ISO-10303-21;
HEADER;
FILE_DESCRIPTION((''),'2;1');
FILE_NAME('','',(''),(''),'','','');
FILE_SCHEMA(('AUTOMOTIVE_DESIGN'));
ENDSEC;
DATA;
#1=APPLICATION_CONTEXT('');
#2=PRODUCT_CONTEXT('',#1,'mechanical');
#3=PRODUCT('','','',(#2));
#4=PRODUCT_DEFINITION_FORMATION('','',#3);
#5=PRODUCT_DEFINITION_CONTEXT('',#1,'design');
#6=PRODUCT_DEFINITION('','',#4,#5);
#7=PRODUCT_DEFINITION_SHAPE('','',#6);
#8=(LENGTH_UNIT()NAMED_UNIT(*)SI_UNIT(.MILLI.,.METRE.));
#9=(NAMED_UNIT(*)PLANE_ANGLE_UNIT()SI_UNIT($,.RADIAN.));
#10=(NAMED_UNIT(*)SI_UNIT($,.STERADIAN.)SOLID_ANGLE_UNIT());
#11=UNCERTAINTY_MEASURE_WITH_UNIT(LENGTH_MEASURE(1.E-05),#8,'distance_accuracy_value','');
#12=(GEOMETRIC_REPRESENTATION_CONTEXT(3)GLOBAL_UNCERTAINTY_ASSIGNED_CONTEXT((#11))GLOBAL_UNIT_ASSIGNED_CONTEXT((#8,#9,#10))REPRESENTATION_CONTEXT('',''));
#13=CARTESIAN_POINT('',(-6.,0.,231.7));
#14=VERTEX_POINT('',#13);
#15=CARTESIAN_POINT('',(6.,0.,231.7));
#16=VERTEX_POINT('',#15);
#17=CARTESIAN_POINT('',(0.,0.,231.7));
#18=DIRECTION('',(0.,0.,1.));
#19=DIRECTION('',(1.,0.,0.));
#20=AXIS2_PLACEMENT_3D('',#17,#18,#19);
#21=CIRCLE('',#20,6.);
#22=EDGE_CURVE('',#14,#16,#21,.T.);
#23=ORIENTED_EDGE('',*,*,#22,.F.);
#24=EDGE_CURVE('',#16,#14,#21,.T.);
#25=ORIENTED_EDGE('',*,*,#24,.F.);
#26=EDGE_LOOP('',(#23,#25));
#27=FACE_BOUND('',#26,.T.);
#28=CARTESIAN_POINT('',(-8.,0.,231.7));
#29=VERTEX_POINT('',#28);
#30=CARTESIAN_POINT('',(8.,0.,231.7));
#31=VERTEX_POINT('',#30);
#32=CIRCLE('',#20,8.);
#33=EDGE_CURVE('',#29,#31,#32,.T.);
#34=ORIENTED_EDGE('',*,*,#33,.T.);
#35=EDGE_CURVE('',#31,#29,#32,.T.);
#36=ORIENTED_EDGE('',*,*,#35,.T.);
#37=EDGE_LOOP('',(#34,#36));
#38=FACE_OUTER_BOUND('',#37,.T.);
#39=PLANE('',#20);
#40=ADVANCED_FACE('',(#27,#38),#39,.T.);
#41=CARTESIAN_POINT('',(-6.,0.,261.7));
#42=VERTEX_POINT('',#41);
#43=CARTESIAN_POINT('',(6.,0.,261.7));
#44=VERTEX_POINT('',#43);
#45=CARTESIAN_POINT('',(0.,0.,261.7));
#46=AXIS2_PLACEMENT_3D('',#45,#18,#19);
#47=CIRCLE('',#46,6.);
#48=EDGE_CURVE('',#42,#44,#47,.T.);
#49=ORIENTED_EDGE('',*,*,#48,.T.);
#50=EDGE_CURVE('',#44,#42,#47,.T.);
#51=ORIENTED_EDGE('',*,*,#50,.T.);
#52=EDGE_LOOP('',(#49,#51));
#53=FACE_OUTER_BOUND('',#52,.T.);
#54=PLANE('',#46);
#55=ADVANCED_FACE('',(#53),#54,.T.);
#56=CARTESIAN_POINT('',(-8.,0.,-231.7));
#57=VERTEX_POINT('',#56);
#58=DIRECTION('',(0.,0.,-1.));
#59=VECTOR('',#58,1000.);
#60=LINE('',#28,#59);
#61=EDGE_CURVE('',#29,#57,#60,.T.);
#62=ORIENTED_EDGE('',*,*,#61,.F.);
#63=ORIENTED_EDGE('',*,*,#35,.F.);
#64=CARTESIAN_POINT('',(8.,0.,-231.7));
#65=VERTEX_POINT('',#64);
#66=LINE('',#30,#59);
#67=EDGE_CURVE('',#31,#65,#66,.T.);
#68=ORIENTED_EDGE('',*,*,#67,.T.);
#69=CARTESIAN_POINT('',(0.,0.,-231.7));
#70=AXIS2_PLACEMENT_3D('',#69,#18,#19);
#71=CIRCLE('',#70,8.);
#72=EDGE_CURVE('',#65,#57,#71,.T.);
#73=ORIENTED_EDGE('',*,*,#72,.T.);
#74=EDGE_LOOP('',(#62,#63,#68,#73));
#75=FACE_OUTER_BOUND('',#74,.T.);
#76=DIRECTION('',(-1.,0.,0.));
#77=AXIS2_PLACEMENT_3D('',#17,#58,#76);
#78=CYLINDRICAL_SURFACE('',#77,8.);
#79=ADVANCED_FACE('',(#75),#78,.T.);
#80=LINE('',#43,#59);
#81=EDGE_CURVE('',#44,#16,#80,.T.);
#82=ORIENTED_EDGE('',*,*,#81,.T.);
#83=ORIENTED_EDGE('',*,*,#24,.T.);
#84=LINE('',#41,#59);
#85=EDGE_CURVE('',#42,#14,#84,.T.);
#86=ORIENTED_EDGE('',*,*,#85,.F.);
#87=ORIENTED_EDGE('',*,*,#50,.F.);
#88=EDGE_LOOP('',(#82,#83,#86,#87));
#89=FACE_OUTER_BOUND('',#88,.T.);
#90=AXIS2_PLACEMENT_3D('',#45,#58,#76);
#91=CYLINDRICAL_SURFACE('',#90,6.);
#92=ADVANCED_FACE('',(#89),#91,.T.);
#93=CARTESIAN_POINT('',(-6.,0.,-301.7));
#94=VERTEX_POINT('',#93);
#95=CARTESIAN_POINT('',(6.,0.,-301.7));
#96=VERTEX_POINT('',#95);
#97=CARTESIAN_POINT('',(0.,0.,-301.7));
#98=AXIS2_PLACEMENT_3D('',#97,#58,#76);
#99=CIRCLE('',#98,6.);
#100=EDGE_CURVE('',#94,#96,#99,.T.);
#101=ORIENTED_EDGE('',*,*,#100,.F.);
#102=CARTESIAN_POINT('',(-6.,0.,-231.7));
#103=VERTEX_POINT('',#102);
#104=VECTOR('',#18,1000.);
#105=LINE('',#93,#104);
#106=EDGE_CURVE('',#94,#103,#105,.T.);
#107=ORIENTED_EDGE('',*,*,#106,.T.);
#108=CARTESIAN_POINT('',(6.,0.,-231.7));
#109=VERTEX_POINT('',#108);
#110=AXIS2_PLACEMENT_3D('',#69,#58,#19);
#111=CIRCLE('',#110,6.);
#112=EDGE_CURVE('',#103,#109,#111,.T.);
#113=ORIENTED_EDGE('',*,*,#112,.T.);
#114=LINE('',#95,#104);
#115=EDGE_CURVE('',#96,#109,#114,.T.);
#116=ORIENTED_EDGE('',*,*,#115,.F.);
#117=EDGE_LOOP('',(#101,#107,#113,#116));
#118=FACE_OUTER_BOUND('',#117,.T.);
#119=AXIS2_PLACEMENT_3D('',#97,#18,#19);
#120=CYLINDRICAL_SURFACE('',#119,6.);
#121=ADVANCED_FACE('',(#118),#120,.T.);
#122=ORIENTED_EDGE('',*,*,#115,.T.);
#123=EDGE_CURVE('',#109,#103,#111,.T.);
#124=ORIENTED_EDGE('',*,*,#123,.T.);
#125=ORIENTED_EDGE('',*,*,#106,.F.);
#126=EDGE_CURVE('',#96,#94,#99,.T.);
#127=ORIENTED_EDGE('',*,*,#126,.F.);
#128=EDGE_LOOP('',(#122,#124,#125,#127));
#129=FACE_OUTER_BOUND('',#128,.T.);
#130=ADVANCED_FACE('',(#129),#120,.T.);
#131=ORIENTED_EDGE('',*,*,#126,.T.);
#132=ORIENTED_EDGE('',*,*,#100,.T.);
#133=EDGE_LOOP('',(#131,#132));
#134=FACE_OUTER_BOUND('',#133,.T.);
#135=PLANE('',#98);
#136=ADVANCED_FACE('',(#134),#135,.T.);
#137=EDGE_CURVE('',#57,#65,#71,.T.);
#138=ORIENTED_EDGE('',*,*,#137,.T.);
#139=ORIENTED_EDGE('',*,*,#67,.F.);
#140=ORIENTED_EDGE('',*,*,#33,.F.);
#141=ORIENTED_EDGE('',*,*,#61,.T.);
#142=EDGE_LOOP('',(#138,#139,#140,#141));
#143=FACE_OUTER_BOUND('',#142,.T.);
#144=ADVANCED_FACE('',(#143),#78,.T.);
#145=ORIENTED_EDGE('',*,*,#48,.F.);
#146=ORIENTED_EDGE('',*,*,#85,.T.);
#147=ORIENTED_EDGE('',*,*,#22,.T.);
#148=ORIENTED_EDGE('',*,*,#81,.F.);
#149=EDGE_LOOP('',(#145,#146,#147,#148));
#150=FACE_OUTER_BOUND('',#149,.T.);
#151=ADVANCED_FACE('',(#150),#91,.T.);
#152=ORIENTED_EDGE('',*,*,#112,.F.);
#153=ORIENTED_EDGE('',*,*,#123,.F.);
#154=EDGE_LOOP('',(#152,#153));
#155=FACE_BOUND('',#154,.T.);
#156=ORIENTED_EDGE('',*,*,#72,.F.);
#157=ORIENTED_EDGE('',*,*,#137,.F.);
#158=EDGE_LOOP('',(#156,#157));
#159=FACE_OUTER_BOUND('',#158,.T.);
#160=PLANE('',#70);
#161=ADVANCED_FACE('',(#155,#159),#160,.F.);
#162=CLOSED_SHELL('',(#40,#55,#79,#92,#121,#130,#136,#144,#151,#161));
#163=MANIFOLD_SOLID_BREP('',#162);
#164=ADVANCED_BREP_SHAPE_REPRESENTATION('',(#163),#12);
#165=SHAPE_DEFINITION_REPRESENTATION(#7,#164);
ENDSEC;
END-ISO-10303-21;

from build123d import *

# Parameters (mm, degrees)
SKETCH1_R           = 8
BOSS_EXTRUDE1_DEPTH = 231.7
SKETCH2_R           = 6
BOSS_EXTRUDE2_DEPTH = 30
BOSS_EXTRUDE3_START = 70
SKETCH4_R           = 6
BOSS_EXTRUDE3_DEPTH = 70


with BuildPart() as part:
    # Sketch1 → Boss-Extrude1 (new, symmetric)
    with BuildSketch(Plane.XY):
        with Locations(Location((0, 0, 0), (0, 0, 180))):
            Circle(SKETCH1_R)
    extrude(amount=BOSS_EXTRUDE1_DEPTH, both=True)

    # Sketch2 → Boss-Extrude2 (add)
    with BuildSketch(Plane.XY.offset(231.7)):
        Circle(SKETCH2_R)
    extrude(amount=BOSS_EXTRUDE2_DEPTH)

    # Sketch4 → Boss-Extrude3 (add)
    with BuildSketch(Plane(origin=(0, 0, -231.7), x_dir=(-1, 0, 0), z_dir=(0, 0, -1)).offset(BOSS_EXTRUDE3_START)):
        with Locations(Location((0, 0, 0), (0, 0, 180))):
            Circle(SKETCH4_R)
    extrude(amount=-BOSS_EXTRUDE3_DEPTH)


solid = part.part
